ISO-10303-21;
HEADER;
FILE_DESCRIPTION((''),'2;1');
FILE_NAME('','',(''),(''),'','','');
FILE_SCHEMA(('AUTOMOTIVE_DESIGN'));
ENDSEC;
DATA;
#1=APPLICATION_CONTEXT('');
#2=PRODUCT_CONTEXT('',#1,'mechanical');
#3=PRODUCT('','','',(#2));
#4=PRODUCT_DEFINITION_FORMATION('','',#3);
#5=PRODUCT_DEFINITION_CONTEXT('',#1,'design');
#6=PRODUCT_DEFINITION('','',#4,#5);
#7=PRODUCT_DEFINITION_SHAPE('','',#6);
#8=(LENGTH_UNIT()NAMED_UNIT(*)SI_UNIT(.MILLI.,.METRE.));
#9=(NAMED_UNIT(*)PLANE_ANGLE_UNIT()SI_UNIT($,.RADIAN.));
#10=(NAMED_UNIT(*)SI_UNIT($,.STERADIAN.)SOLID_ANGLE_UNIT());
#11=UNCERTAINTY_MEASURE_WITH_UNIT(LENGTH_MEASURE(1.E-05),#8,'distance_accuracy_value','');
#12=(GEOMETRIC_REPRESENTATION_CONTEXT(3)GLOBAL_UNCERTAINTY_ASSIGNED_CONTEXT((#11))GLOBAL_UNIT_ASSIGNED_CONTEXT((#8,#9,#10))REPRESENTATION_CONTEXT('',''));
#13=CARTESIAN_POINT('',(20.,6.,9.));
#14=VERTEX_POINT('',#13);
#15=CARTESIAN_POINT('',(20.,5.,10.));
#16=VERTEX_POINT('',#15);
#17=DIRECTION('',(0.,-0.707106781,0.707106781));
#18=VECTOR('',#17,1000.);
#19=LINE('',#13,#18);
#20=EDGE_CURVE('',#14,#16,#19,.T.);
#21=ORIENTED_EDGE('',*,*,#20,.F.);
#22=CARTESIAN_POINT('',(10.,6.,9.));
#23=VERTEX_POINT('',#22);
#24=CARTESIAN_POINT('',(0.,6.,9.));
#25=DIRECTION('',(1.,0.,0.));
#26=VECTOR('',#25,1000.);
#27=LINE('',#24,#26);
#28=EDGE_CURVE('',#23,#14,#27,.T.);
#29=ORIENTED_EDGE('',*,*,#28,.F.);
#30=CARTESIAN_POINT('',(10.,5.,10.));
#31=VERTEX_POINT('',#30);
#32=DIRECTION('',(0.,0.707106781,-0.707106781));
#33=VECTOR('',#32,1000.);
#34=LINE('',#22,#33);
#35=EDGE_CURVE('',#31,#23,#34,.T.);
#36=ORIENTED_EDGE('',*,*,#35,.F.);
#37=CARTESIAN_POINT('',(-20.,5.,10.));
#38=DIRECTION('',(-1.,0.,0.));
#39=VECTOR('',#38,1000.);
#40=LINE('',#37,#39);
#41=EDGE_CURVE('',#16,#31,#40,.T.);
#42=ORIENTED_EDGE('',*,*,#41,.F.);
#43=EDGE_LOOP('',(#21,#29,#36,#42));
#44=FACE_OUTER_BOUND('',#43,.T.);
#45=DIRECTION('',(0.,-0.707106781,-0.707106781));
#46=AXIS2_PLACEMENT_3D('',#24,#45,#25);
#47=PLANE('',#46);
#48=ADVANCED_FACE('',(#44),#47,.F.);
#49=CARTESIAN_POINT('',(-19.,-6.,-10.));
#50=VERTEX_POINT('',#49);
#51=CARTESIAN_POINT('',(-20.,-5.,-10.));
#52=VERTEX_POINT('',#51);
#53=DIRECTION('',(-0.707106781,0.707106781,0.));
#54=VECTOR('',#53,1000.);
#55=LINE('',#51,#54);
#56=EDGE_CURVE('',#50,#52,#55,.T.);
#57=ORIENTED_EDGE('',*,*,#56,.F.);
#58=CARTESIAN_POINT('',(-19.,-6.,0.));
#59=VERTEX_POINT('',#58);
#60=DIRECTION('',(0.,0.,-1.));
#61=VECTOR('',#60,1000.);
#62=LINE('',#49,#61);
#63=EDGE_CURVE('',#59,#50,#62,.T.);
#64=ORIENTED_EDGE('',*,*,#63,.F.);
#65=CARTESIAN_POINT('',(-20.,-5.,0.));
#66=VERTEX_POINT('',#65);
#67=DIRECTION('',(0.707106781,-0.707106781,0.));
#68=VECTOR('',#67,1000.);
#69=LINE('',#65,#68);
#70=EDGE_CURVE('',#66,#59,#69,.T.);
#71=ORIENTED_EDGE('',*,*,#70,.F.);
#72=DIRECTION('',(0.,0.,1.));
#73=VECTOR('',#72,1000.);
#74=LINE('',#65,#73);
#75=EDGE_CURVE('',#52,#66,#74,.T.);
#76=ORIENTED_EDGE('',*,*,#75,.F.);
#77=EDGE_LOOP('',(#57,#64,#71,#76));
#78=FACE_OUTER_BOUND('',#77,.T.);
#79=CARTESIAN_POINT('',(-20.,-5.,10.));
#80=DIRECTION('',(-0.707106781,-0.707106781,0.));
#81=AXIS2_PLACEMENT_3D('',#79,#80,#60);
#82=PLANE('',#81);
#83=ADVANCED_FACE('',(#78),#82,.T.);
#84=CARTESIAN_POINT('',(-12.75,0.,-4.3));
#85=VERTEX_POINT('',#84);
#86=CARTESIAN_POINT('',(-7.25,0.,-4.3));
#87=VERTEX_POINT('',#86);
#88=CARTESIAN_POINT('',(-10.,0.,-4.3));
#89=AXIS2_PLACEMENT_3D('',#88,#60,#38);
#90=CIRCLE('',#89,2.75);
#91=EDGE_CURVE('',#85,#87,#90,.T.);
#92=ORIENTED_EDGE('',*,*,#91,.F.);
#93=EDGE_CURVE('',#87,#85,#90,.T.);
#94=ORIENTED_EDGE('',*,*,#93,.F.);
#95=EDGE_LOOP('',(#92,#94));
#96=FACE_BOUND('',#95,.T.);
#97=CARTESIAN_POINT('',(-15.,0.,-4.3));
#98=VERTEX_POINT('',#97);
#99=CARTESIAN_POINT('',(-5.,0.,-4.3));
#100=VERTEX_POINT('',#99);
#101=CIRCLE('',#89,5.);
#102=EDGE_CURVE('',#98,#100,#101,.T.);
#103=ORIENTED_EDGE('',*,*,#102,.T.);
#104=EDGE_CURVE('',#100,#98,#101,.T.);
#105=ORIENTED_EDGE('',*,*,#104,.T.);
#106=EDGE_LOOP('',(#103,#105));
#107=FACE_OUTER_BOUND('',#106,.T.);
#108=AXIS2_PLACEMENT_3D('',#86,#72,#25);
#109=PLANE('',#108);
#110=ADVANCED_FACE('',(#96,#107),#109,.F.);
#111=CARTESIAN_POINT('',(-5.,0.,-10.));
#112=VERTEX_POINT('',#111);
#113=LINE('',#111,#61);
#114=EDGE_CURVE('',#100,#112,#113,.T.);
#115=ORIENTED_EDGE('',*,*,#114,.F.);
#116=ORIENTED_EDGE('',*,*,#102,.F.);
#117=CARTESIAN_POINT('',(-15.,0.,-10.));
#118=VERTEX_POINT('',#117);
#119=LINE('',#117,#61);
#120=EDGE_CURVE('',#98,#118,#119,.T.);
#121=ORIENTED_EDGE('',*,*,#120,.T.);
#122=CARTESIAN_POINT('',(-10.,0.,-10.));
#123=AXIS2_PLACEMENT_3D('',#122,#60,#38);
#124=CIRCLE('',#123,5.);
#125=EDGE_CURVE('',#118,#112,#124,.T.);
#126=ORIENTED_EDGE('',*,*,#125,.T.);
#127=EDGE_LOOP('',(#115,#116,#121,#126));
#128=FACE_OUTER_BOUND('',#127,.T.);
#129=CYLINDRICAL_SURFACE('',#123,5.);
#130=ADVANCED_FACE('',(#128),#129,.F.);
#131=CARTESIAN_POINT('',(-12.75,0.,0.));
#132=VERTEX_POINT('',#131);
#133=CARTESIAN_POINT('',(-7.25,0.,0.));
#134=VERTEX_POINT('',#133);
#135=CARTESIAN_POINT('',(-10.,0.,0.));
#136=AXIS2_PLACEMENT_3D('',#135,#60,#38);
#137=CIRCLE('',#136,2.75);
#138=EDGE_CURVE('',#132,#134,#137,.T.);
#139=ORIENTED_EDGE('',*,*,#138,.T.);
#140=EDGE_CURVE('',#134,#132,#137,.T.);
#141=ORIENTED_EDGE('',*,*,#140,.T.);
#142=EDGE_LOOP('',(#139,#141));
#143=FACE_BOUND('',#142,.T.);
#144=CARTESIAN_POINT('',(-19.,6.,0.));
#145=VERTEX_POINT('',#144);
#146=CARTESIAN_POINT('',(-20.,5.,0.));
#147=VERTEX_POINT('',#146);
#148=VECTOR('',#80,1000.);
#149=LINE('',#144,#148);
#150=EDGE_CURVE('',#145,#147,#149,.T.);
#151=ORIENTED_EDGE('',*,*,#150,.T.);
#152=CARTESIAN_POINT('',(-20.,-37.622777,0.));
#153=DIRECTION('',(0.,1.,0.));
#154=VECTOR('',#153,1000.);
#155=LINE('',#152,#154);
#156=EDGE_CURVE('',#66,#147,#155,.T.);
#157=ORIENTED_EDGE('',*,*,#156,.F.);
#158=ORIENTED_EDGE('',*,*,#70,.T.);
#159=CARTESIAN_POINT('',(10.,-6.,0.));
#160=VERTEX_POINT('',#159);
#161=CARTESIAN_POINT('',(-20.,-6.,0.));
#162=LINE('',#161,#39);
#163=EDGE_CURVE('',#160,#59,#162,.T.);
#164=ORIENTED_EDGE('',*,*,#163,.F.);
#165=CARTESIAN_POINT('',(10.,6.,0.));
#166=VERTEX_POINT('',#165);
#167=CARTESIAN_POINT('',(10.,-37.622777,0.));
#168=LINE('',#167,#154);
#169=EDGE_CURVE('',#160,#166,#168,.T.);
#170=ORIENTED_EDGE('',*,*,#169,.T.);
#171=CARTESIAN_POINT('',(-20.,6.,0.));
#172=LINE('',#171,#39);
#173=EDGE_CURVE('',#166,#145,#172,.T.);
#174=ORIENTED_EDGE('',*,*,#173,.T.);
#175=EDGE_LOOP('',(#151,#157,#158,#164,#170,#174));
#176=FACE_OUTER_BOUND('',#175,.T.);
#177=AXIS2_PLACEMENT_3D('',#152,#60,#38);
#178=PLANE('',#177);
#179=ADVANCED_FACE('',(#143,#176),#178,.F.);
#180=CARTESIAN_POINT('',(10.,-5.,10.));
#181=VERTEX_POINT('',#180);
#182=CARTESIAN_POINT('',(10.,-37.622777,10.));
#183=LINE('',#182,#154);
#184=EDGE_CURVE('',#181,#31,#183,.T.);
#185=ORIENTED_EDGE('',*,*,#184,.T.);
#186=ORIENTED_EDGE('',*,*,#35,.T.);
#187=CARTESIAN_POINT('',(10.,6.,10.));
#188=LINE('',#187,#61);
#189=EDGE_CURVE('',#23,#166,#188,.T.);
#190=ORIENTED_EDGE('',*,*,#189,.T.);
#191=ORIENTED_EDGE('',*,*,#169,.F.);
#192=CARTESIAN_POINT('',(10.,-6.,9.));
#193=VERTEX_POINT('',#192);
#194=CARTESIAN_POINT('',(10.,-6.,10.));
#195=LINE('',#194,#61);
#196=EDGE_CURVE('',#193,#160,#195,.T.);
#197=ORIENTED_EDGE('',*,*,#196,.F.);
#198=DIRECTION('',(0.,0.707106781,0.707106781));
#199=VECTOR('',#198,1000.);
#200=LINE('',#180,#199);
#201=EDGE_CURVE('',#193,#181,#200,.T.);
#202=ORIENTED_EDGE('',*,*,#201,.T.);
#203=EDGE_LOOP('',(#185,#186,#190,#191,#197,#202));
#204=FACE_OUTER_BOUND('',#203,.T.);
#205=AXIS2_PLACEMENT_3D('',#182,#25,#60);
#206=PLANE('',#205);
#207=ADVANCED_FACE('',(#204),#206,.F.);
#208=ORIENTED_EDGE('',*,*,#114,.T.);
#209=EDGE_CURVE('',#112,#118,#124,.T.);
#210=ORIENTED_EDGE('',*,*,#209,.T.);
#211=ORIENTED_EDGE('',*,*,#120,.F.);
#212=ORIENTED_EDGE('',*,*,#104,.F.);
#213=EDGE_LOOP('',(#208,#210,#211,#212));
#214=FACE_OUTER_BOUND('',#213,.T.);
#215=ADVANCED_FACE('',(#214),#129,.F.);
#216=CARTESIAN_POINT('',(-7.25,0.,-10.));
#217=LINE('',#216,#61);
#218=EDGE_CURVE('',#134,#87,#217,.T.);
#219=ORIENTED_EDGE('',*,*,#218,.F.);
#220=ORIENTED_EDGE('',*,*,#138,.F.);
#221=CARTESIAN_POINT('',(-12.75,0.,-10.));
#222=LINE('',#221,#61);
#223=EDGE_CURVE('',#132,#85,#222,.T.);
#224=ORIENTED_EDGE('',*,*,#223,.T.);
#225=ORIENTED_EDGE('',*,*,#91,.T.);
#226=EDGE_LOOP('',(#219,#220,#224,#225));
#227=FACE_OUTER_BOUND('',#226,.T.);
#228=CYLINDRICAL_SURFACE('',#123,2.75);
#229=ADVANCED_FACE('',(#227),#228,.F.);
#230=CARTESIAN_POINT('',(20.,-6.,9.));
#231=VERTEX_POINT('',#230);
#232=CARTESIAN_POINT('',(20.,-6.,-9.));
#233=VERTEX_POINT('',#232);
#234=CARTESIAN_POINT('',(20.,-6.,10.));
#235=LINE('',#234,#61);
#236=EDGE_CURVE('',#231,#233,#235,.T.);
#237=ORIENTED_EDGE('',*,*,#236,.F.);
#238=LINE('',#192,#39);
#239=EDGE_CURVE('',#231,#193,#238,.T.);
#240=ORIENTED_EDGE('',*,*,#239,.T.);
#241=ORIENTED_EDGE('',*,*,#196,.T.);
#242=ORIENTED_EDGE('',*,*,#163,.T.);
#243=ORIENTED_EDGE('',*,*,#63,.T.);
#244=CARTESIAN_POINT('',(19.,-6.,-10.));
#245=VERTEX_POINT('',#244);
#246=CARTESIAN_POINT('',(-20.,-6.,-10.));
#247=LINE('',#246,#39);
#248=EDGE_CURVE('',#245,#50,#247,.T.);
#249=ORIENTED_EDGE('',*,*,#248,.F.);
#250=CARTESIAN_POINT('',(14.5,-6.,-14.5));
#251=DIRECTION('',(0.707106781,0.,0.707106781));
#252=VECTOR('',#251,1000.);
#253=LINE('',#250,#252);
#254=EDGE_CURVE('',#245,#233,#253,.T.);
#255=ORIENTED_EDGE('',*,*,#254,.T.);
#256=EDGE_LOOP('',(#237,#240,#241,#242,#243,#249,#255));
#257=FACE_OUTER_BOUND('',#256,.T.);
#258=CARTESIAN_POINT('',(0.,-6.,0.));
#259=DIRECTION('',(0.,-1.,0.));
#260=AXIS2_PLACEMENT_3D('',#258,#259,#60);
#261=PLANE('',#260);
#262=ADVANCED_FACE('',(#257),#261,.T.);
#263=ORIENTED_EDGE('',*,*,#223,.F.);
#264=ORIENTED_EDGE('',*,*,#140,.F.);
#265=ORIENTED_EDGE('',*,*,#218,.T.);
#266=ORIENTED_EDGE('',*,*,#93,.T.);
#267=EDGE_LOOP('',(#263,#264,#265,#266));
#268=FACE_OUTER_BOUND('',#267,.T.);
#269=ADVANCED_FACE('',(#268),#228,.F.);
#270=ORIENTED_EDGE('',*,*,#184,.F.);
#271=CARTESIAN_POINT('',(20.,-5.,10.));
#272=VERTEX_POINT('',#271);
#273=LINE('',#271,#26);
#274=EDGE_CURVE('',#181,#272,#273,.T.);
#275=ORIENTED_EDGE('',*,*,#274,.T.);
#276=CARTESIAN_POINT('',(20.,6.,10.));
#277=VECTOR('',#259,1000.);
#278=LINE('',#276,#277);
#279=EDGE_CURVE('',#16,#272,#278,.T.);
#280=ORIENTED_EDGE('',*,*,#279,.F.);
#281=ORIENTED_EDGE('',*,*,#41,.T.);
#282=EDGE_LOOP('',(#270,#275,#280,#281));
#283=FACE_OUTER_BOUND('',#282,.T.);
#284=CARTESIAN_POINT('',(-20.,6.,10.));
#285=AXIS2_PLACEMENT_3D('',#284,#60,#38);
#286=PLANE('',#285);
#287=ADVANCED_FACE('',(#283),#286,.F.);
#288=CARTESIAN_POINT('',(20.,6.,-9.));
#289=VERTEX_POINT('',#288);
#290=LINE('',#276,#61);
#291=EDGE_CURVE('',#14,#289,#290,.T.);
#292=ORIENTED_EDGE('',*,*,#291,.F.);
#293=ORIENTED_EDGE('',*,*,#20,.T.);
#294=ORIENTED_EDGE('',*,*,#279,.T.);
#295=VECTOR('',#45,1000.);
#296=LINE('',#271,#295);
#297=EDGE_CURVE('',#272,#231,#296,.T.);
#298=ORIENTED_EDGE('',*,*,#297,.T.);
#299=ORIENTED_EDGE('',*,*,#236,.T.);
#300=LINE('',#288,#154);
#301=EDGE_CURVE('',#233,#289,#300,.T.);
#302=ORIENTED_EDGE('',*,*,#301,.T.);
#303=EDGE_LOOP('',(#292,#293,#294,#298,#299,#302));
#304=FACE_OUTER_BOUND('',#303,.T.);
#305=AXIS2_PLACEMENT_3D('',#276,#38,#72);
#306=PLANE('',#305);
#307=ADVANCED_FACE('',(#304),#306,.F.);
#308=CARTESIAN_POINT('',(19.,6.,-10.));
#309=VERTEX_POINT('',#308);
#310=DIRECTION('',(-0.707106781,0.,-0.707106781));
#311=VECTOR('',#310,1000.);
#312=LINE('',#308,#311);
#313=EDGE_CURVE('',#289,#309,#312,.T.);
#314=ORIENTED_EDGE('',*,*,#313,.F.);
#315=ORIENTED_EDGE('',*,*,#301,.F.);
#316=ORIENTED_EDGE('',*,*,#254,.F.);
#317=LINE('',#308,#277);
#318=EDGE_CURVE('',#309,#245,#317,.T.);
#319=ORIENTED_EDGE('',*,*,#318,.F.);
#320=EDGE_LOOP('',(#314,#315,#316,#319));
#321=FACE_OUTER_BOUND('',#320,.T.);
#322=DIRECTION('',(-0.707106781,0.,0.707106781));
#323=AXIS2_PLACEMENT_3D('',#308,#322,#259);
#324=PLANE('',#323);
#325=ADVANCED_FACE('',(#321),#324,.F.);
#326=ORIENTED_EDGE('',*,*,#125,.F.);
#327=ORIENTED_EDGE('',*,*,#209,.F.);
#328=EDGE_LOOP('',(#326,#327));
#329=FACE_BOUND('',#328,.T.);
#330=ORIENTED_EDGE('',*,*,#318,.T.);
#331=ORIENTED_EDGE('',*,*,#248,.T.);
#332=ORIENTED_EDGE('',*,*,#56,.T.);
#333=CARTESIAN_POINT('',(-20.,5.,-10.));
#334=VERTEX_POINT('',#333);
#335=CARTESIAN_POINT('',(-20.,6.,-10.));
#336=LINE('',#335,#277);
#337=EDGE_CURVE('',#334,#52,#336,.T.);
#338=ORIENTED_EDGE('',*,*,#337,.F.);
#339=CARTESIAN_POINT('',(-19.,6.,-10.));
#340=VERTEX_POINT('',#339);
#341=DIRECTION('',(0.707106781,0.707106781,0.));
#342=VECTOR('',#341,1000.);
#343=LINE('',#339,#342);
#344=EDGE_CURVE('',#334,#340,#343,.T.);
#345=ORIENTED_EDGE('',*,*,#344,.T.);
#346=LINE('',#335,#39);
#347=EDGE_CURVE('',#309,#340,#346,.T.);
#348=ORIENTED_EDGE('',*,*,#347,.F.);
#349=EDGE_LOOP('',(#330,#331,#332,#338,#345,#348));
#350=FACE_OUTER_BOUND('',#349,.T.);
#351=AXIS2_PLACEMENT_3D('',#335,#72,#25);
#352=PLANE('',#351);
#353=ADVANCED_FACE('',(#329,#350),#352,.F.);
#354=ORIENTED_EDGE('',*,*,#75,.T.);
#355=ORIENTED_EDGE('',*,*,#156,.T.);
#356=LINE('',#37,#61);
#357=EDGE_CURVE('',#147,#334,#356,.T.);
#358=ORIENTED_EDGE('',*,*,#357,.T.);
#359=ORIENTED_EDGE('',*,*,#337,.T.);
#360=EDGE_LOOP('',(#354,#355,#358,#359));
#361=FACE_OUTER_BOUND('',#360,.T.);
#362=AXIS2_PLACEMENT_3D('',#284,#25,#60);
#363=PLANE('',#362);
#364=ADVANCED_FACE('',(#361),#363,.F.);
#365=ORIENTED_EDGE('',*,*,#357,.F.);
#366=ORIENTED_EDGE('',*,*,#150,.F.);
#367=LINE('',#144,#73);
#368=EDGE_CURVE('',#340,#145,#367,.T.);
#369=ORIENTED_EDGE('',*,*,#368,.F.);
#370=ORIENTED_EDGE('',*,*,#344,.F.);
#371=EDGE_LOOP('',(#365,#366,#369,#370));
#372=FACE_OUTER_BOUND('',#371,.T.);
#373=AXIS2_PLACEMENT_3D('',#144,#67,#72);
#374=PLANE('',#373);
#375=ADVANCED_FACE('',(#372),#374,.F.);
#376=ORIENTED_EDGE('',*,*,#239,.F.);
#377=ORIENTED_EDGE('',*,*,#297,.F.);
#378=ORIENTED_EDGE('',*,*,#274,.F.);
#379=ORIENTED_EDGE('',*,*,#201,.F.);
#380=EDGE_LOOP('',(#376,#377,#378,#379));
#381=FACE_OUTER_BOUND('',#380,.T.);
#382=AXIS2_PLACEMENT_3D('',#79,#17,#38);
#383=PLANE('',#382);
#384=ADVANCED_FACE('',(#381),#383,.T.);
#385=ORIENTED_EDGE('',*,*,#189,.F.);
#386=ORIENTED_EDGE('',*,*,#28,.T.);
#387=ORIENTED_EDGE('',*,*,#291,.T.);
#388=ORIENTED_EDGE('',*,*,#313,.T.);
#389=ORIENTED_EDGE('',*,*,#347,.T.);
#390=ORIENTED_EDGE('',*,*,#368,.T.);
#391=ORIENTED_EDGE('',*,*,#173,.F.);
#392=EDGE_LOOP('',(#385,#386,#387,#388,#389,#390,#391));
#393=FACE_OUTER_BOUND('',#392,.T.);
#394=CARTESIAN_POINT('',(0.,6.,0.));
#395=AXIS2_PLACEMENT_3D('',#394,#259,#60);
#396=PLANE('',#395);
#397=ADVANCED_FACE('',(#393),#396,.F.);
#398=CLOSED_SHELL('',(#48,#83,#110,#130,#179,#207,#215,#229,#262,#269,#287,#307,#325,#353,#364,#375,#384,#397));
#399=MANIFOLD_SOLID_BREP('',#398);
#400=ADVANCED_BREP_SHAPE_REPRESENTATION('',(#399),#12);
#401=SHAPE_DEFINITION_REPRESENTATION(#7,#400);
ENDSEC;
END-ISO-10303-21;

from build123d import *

# Parameters (mm, degrees)
SKETCH_1_W                = 40
SKETCH_1_H                = 20
EXTRUDE_1_DEPTH           = 6
SKETCH_2_W                = 30
SKETCH_2_H                = 10
CUT_EXTRUDE_1_DEPTH       = 12
HOLE_WIZARD_1_D           = 5.5
HOLE_WIZARD_1_CBORE_D     = 10
HOLE_WIZARD_1_CBORE_DEPTH = 5.7
CHAMFER_1_SIZE            = 1


with BuildPart() as part:
    # 草图1 → 凸台-拉伸1 (new, symmetric)
    with BuildSketch(Plane(origin=(0, 0, 0), x_dir=(1, 0, 0), z_dir=(0, 1, 0))):
        Rectangle(SKETCH_1_W, SKETCH_1_H)
    extrude(amount=EXTRUDE_1_DEPTH, both=True)

    # 草图2 → 切除-拉伸1 (cut)
    with BuildSketch(Plane(origin=(0, 6, 0), x_dir=(1, 0, 0), z_dir=(0, 1, 0))):
        with Locations((-5, -5)):
            Rectangle(SKETCH_2_W, SKETCH_2_H)
    extrude(amount=-CUT_EXTRUDE_1_DEPTH, mode=Mode.SUBTRACT)

    # 打孔尺寸(%根据)内六角圆柱头螺钉的类型1 (through all)
    with Locations(Plane(origin=(0, 0, -10), x_dir=(-1, 0, 0), z_dir=(0, 0, -1))):
        with Locations((10, 0)):
            CounterBoreHole(HOLE_WIZARD_1_D / 2, HOLE_WIZARD_1_CBORE_D / 2, HOLE_WIZARD_1_CBORE_DEPTH)

    # 倒角1
    chamfer_1_edges = [part.edges().sort_by_distance(p)[0] for p in [
        (-20, 6, -5),
        (15, -6, 10),
        (15, 6, 10),
        (-20, -6, -5),
        (20, 0, -10),
    ]]
    chamfer(chamfer_1_edges, length=CHAMFER_1_SIZE)


solid = part.part
